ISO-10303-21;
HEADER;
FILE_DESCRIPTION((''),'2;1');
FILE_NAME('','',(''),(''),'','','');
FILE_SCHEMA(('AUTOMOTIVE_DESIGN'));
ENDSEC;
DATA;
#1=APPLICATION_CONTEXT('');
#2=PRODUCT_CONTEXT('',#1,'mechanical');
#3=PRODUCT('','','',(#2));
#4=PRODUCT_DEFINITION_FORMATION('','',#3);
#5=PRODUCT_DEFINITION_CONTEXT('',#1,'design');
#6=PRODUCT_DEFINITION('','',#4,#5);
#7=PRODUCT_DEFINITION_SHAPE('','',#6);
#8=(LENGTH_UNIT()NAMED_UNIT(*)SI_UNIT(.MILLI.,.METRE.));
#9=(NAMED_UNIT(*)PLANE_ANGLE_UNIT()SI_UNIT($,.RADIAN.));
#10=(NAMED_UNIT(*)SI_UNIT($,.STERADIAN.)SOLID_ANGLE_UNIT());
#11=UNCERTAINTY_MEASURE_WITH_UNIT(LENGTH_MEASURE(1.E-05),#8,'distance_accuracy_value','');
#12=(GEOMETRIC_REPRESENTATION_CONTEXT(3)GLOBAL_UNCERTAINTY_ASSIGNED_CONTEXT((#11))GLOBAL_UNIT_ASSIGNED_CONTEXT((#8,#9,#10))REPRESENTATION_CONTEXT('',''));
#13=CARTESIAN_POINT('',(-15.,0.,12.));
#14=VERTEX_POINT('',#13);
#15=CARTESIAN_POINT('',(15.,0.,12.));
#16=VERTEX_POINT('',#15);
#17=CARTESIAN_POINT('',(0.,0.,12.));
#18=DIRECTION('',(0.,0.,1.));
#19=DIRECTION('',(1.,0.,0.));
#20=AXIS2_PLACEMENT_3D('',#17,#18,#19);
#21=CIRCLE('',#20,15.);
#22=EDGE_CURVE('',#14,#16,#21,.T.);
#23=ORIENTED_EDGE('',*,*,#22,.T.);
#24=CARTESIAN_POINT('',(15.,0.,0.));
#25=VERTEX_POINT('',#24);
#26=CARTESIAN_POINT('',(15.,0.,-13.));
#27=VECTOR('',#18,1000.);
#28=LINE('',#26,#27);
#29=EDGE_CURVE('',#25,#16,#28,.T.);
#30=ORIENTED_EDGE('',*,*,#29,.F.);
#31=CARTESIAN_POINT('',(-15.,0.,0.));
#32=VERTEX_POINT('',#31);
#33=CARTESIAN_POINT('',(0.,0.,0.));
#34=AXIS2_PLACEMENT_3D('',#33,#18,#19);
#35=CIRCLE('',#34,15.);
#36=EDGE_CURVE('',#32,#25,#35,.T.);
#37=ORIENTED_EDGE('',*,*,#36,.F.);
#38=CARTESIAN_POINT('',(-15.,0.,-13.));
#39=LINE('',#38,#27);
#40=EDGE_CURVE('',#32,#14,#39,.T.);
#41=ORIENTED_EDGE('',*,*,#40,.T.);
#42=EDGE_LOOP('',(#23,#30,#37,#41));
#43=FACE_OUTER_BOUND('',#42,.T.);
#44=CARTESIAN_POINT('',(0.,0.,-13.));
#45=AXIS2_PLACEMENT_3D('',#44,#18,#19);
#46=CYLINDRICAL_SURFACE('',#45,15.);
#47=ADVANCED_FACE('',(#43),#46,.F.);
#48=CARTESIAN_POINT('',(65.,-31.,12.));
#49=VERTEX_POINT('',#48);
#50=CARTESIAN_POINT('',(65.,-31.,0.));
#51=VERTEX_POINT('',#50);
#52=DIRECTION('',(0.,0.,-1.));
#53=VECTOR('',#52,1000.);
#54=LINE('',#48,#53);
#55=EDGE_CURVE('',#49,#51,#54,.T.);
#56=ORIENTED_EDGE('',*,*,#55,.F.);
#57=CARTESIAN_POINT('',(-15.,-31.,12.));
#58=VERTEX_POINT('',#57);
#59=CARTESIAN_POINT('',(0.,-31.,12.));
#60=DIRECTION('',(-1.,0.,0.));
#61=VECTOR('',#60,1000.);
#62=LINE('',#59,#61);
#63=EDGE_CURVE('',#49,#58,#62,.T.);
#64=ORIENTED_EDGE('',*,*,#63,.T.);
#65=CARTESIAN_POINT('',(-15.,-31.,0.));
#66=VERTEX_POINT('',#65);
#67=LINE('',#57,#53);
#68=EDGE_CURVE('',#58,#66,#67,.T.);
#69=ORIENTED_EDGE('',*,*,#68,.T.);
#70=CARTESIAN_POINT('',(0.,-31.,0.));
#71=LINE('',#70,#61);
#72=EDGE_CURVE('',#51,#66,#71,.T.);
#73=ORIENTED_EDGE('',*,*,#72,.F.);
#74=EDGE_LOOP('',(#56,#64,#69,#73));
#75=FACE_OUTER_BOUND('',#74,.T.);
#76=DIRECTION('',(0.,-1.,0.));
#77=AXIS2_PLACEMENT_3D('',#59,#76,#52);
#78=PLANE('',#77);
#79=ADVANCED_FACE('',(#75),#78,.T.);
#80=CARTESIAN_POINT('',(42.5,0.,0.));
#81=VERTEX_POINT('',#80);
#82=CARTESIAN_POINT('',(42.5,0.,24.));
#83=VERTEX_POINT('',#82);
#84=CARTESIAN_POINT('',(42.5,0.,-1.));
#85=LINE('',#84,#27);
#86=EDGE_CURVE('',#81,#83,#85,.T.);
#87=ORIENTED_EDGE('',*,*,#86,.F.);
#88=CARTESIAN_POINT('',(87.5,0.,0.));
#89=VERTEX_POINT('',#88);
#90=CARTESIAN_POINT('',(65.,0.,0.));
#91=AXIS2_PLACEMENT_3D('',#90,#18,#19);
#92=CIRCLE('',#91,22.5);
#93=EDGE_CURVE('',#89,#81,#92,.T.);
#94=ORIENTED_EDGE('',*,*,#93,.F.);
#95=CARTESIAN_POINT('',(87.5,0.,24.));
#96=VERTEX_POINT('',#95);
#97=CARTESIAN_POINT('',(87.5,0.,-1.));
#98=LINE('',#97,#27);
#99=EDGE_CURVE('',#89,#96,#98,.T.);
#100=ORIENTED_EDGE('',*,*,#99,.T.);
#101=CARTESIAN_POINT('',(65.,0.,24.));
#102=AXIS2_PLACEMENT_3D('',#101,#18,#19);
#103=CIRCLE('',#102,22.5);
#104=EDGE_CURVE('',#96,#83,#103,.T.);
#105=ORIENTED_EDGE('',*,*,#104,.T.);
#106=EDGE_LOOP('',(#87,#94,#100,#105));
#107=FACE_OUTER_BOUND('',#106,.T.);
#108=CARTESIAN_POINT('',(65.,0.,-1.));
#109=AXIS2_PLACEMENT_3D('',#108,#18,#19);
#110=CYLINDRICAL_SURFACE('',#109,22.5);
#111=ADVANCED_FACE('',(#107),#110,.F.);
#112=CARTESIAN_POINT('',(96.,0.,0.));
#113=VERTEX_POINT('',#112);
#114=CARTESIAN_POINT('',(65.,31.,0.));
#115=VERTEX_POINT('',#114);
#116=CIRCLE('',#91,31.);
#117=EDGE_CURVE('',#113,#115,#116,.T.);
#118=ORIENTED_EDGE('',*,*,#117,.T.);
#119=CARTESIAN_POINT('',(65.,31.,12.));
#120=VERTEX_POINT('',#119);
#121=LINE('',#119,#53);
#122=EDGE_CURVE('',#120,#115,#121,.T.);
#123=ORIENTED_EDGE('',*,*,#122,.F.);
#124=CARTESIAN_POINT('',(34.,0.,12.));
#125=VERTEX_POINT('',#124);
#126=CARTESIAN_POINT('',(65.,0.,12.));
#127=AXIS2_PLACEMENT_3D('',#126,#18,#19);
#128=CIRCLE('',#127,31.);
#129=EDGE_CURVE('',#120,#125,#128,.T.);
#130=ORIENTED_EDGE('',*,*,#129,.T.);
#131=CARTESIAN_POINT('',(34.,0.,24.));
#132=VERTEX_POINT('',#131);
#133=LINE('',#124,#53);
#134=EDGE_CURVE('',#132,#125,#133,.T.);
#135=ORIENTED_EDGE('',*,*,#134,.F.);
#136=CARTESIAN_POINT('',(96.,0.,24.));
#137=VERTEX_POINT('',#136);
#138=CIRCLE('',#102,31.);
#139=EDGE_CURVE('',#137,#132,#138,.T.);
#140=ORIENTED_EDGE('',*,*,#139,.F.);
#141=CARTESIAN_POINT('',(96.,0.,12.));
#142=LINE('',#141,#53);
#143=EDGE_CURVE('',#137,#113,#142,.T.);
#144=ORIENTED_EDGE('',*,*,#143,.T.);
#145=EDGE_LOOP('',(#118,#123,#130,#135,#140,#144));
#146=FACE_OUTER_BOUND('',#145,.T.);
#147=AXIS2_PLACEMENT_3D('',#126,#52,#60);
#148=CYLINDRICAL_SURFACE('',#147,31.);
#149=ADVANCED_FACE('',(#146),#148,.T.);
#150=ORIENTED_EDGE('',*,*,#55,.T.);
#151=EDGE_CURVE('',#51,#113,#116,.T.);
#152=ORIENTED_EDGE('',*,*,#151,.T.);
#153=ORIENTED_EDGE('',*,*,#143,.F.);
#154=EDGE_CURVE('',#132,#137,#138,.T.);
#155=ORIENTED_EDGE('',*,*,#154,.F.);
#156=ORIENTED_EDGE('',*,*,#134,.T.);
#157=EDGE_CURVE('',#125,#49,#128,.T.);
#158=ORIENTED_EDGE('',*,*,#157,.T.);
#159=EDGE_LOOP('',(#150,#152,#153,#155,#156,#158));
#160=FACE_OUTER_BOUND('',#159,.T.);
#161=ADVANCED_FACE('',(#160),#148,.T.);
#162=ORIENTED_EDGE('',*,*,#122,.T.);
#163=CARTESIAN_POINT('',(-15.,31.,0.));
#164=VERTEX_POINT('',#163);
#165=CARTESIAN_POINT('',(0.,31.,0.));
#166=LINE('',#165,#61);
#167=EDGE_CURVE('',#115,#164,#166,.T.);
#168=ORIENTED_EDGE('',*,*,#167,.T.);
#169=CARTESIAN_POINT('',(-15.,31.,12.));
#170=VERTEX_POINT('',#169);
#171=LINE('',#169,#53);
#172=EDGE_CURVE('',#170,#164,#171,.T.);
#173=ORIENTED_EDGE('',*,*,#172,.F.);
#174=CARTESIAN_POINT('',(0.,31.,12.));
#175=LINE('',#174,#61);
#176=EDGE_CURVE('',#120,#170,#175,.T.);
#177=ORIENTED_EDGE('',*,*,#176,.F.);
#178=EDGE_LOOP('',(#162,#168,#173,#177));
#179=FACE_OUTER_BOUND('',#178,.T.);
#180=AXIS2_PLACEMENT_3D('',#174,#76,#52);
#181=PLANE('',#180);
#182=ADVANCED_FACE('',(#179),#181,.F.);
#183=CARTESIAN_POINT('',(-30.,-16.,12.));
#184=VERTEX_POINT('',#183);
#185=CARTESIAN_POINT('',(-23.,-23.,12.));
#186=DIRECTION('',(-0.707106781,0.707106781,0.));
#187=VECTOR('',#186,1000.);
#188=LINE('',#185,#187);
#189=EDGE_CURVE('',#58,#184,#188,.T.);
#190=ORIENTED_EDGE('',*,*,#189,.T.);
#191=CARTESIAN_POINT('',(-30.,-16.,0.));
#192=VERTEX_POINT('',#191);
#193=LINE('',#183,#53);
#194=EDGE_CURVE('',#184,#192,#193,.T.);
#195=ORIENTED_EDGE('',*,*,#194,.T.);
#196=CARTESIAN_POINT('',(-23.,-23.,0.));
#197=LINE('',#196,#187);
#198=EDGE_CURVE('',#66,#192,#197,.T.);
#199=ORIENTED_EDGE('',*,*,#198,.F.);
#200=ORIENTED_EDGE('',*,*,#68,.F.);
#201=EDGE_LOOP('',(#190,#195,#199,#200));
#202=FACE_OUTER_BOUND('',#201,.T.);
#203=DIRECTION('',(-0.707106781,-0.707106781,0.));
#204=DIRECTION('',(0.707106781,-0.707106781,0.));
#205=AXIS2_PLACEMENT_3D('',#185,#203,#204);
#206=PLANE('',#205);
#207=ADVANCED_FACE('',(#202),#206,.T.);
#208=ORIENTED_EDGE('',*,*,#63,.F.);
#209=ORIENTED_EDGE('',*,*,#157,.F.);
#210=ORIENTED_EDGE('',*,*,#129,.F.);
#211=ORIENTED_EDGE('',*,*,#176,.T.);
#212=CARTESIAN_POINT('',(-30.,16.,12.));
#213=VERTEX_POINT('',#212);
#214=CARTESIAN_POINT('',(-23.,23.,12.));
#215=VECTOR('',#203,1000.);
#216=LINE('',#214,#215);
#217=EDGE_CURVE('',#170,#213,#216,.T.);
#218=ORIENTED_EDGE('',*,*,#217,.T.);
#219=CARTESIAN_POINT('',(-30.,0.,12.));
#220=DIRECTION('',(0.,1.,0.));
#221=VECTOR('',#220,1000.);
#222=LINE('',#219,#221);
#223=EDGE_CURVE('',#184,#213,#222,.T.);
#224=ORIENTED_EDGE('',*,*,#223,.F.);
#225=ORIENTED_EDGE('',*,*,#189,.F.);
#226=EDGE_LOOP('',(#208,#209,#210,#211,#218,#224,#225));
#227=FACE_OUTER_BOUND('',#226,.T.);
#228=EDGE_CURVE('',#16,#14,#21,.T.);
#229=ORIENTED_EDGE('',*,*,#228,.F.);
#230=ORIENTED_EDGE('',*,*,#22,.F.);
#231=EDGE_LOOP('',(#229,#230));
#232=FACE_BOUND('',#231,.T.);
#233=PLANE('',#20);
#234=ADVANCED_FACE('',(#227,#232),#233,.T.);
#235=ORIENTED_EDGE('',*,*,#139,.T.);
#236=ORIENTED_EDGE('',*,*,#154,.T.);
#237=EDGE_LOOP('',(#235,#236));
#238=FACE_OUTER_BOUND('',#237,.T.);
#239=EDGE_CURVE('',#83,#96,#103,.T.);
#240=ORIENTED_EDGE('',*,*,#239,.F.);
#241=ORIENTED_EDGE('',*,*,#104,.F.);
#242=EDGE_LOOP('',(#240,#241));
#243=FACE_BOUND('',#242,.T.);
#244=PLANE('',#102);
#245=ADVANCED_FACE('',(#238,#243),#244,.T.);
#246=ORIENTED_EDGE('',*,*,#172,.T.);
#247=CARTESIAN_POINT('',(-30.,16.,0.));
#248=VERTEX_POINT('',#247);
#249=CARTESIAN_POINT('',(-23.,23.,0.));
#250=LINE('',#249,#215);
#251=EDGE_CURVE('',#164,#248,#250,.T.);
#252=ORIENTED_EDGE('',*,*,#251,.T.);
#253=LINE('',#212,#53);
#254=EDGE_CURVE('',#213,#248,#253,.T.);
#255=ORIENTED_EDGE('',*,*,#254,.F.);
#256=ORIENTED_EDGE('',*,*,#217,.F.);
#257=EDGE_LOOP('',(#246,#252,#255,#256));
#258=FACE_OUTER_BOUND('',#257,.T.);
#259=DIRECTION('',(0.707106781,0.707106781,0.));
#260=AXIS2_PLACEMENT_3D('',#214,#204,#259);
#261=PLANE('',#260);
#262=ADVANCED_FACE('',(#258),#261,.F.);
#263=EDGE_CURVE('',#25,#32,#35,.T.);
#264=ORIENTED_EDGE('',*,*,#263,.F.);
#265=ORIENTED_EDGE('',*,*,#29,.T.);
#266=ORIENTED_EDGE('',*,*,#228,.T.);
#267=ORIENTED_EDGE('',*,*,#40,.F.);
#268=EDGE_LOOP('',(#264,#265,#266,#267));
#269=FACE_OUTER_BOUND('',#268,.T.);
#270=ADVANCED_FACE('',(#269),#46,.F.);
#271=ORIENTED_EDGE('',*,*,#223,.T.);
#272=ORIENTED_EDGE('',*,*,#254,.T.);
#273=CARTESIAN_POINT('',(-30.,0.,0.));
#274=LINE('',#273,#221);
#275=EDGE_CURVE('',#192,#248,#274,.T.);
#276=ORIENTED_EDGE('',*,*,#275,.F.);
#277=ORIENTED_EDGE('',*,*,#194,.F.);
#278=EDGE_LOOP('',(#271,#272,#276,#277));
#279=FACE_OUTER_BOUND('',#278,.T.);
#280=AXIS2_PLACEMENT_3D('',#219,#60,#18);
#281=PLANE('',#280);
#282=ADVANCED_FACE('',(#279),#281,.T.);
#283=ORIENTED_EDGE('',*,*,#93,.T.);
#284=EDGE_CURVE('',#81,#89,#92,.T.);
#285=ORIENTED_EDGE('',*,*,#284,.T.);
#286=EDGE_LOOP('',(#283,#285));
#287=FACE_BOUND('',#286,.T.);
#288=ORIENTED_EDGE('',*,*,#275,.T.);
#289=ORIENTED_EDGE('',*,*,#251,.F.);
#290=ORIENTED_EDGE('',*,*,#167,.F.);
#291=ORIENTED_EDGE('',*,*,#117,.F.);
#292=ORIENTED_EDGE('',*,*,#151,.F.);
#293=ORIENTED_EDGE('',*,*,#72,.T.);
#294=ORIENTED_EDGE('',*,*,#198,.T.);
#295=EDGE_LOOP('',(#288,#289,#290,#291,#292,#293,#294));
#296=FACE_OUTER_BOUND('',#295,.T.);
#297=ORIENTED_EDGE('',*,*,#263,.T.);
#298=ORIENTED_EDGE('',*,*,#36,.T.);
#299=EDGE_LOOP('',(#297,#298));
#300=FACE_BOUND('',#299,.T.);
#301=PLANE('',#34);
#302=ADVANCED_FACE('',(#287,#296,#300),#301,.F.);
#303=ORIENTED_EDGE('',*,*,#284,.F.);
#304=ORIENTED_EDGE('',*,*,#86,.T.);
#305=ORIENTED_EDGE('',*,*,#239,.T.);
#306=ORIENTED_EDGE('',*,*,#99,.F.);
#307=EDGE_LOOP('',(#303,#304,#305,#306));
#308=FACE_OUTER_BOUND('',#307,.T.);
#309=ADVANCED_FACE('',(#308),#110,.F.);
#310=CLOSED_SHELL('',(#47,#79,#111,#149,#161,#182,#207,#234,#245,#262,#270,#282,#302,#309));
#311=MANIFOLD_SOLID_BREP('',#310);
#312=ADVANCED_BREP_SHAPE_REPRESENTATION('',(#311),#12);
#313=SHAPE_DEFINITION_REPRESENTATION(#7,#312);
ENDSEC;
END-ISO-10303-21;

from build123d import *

# Parameters (mm, degrees)
BASE_PLATE_DEPTH = 12
BOSS_SKETCH_62_R = 31
BOSS_62_DEPTH    = 12
BORE_SKETCH_45_R = 22.5
BORE_45_DEPTH    = 25
HOLE_SKETCH_30_R = 15
HOLE_30_DEPTH    = 25


with BuildPart() as part:
    # Base Plate Sketch → Base Plate (new body)
    with BuildSketch(Plane.XY):
        with BuildLine():
            Line((-15, -31), (65, -31))
            ThreePointArc((65, -31), (96, 0), (65, 31))
            Line((65, 31), (-15, 31))
            Line((-15, 31), (-30, 16))
            Line((-30, 16), (-30, 0))
            Line((-30, 0), (-30, -16))
            Line((-30, -16), (-15, -31))
        make_face()
    extrude(amount=BASE_PLATE_DEPTH)

    # Boss Sketch Ø62 → Boss Ø62 (add)
    with BuildSketch(Plane.XY.offset(12)):
        with Locations(Location((65, 0, 0), (0, 0, 90))):
            Circle(BOSS_SKETCH_62_R)
    extrude(amount=BOSS_62_DEPTH)

    # Bore Sketch Ø45 → Bore Ø45 (cut)
    with BuildSketch(Plane.XY.offset(24)):
        with Locations((65, 0)):
            Circle(BORE_SKETCH_45_R)
    extrude(amount=-BORE_45_DEPTH, mode=Mode.SUBTRACT)

    # Hole Sketch Ø30 → Hole Ø30 (cut)
    with BuildSketch(Plane.XY.offset(12)):
        Circle(HOLE_SKETCH_30_R)
    extrude(amount=-HOLE_30_DEPTH, mode=Mode.SUBTRACT)


solid = part.part
